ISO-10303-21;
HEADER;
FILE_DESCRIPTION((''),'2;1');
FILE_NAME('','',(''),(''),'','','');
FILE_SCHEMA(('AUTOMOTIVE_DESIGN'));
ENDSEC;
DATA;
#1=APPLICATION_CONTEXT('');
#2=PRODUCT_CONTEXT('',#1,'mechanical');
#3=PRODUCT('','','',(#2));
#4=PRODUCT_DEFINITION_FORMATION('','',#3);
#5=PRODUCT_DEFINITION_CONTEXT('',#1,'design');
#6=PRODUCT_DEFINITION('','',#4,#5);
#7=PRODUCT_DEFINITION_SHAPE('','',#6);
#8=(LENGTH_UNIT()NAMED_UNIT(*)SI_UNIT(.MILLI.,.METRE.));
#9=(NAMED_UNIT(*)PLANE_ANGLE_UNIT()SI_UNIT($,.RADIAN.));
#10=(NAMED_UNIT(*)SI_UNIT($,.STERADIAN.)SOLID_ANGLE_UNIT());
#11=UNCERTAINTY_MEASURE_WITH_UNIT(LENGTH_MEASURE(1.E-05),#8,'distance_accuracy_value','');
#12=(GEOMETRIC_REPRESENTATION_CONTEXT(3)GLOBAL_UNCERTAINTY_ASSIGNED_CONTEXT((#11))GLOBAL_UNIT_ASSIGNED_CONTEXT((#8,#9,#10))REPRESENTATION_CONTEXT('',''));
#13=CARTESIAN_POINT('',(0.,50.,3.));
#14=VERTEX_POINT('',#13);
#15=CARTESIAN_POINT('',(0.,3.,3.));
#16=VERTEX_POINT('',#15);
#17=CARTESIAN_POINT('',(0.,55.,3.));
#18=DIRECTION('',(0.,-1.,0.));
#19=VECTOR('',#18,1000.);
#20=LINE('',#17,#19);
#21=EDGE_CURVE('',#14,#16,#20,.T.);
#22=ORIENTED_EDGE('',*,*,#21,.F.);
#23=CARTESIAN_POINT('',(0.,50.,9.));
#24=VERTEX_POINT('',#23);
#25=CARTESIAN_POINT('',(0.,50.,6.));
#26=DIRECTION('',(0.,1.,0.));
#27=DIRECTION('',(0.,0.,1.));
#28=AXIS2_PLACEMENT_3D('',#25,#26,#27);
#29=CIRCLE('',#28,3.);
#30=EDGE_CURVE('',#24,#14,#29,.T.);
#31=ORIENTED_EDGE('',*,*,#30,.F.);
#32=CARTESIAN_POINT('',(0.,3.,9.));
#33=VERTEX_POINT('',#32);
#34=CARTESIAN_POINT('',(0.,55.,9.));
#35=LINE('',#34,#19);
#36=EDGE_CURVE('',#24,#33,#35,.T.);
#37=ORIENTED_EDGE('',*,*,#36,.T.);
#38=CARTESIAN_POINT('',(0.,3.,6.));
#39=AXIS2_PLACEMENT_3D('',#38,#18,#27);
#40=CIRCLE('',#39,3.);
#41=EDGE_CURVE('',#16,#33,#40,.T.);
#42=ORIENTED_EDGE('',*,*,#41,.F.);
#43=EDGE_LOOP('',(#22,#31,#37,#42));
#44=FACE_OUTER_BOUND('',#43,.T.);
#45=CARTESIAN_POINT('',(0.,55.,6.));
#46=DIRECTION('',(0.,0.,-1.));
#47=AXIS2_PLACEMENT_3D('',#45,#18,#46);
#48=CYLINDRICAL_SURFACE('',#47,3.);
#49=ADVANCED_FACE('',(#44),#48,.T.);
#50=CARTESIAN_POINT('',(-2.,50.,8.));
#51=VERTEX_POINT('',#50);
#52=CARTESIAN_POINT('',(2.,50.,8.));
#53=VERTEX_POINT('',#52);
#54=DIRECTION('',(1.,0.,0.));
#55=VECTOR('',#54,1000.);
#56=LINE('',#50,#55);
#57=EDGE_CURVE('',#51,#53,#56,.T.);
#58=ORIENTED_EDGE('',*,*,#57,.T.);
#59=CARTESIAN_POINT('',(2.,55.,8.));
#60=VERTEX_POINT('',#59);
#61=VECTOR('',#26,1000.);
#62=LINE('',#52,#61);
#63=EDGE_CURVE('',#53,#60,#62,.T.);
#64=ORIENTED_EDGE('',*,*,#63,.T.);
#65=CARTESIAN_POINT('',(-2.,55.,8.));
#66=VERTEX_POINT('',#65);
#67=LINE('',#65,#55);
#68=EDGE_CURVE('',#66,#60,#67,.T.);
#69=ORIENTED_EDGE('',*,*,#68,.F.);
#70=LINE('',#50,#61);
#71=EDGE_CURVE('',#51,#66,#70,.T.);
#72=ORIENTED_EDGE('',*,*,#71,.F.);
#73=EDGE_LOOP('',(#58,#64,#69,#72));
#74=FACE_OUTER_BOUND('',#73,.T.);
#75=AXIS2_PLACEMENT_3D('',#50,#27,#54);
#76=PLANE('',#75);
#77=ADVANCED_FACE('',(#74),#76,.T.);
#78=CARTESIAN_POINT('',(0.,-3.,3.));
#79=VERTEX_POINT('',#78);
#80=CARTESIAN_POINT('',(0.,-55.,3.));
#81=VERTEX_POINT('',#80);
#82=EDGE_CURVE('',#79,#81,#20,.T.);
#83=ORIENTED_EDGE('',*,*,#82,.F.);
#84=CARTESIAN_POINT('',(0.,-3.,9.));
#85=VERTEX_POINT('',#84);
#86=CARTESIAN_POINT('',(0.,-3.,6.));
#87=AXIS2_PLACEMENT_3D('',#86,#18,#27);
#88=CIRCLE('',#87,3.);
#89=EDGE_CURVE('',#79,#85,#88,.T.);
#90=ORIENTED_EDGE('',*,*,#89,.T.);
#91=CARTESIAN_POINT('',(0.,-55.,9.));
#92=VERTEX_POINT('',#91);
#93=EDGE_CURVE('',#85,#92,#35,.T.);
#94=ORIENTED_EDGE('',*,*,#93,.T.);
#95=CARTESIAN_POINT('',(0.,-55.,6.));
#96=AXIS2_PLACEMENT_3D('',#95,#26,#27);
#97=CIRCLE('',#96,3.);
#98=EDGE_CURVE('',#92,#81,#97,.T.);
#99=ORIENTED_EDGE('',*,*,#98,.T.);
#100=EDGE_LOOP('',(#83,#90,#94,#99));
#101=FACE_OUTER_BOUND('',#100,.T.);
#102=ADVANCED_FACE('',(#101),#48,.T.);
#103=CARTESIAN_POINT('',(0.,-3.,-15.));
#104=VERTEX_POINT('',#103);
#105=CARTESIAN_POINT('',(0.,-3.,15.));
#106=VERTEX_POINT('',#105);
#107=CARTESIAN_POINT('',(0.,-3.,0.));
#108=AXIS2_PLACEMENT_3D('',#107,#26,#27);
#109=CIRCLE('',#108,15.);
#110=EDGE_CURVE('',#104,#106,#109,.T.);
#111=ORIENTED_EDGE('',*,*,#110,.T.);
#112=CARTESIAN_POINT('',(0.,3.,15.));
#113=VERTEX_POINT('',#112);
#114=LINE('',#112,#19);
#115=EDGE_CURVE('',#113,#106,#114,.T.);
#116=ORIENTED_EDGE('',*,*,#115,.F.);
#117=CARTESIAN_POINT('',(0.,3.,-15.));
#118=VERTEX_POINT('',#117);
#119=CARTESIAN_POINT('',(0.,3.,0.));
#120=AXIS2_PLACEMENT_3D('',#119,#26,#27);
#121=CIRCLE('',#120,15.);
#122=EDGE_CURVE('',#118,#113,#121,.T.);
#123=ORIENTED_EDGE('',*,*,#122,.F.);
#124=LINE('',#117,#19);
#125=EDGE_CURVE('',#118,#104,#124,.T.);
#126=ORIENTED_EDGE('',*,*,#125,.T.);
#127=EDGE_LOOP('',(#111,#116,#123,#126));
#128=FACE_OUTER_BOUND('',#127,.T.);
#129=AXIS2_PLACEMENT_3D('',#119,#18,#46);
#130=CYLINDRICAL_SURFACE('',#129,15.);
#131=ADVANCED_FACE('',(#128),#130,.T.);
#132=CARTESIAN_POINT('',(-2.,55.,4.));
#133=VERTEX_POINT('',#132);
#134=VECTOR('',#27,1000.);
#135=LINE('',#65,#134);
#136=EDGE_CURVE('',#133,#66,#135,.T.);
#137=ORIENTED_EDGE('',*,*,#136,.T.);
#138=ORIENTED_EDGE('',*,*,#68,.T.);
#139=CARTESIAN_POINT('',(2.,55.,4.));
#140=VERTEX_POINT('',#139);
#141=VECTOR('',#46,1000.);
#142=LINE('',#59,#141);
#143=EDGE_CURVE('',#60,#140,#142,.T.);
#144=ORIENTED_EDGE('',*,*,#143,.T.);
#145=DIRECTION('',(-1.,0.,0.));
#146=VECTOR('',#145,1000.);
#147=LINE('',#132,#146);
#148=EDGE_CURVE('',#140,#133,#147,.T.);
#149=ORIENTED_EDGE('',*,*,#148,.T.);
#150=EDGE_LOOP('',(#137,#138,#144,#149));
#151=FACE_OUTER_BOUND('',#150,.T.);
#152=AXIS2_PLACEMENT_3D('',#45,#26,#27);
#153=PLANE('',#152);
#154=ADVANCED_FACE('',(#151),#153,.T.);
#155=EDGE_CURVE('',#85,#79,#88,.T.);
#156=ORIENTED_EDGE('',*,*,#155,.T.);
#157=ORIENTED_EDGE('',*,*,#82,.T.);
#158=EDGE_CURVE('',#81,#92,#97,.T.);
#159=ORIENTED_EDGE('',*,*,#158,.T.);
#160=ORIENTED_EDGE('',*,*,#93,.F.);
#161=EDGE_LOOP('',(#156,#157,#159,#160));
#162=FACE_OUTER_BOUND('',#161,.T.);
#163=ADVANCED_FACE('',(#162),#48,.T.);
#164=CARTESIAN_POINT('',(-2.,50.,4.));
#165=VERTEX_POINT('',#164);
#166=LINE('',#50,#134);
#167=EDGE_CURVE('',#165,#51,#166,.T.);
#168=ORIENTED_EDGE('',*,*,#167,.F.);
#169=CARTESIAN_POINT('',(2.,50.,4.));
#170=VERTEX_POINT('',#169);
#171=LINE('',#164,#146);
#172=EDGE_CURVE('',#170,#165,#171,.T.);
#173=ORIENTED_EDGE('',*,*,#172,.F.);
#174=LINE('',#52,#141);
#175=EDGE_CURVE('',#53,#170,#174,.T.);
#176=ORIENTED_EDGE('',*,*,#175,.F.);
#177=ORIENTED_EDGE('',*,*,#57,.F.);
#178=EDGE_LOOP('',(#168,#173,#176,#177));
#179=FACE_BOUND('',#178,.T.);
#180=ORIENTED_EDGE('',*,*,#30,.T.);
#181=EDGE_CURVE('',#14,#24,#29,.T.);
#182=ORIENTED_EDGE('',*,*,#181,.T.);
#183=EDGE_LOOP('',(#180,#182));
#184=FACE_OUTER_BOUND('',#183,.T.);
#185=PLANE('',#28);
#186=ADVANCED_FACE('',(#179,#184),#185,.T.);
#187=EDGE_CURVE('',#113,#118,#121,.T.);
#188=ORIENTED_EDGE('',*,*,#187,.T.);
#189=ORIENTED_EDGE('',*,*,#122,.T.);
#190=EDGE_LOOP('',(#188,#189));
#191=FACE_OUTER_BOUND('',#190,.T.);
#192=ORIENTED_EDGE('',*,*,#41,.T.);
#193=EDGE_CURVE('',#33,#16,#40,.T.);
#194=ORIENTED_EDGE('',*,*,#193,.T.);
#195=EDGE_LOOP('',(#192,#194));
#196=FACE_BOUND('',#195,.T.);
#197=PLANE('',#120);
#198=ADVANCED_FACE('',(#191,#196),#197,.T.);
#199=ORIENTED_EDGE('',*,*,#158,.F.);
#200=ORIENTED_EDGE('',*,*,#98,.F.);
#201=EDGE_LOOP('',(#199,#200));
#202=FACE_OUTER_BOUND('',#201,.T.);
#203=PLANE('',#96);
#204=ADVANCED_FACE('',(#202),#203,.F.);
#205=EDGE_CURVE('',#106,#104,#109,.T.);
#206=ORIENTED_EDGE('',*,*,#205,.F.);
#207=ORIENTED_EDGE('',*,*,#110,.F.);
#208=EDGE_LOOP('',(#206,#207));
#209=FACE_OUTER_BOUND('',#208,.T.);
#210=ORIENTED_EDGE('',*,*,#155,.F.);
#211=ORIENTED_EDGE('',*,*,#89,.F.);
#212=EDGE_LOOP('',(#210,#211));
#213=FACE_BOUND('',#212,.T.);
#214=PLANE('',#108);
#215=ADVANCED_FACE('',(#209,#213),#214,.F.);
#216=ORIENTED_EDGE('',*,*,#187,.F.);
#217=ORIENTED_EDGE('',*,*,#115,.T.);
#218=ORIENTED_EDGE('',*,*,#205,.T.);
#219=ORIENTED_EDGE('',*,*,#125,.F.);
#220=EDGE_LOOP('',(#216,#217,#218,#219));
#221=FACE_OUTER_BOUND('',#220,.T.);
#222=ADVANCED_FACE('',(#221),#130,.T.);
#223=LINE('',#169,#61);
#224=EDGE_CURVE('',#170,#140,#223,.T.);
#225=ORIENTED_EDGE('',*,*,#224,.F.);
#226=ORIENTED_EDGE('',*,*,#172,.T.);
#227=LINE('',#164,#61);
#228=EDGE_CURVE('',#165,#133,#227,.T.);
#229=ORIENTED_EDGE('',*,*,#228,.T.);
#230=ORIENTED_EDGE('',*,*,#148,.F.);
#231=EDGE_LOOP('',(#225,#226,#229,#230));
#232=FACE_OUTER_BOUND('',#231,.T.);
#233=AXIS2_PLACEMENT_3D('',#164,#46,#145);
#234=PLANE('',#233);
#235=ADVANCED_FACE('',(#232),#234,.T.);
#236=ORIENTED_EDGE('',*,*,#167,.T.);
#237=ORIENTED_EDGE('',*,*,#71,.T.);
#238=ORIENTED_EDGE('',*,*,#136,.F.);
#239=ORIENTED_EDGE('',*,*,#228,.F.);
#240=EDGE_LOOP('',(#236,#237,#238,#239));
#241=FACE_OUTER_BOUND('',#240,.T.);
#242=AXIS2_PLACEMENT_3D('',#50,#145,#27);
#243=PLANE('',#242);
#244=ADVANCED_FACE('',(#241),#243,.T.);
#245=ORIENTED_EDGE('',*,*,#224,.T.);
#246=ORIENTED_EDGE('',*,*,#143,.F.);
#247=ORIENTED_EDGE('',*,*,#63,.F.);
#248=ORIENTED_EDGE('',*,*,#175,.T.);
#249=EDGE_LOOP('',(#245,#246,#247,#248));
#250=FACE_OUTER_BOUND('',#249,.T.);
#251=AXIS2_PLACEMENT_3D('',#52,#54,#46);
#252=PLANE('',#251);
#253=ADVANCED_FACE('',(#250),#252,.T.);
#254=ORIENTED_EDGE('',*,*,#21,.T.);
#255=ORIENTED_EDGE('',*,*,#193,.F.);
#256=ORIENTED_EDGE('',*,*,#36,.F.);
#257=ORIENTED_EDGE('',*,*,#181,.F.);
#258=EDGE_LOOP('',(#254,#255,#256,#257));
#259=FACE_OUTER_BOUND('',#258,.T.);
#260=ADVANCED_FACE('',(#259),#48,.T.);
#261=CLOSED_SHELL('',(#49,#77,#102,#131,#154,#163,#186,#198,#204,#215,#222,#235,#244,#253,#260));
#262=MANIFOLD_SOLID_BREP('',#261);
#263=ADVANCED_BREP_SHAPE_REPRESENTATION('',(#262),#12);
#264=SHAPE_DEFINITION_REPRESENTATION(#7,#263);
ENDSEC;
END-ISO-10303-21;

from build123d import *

# Parameters (mm, degrees)
SKETCH1_R           = 15
BOSS_EXTRUDE1_DEPTH = 3
SKETCH3_R           = 3
BOSS_EXTRUDE2_DEPTH = 55
SKETCH4_R           = 3
SKETCH4_W           = 4
SKETCH4_H           = 4
CUT_EXTRUDE1_DEPTH  = 5


with BuildPart() as part:
    # Sketch1 → Boss-Extrude1 (new, symmetric)
    with BuildSketch(Plane(origin=(0, 0, 0), x_dir=(1, 0, 0), z_dir=(0, 1, 0))):
        with Locations(Location((0, 0, 0), (0, 0, 270))):
            Circle(SKETCH1_R)
    extrude(amount=BOSS_EXTRUDE1_DEPTH, both=True)

    # Sketch3 → Boss-Extrude2 (add, symmetric)
    with BuildSketch(Plane(origin=(0, 0, 0), x_dir=(1, 0, 0), z_dir=(0, 1, 0))):
        with Locations(Location((0, -6, 0), (0, 0, 270))):
            Circle(SKETCH3_R)
    extrude(amount=BOSS_EXTRUDE2_DEPTH, both=True)

    # Sketch4 → Cut-Extrude1 (cut)
    with BuildSketch(Plane(origin=(0, 55, 0), x_dir=(1, 0, 0), z_dir=(0, 1, 0))):
        with Locations(Location((0, -6, 0), (0, 0, 270))):
            Circle(SKETCH4_R)
        with Locations((0, -6)):
            Rectangle(SKETCH4_W, SKETCH4_H, mode=Mode.SUBTRACT)
    extrude(amount=-CUT_EXTRUDE1_DEPTH, mode=Mode.SUBTRACT)


solid = part.part
